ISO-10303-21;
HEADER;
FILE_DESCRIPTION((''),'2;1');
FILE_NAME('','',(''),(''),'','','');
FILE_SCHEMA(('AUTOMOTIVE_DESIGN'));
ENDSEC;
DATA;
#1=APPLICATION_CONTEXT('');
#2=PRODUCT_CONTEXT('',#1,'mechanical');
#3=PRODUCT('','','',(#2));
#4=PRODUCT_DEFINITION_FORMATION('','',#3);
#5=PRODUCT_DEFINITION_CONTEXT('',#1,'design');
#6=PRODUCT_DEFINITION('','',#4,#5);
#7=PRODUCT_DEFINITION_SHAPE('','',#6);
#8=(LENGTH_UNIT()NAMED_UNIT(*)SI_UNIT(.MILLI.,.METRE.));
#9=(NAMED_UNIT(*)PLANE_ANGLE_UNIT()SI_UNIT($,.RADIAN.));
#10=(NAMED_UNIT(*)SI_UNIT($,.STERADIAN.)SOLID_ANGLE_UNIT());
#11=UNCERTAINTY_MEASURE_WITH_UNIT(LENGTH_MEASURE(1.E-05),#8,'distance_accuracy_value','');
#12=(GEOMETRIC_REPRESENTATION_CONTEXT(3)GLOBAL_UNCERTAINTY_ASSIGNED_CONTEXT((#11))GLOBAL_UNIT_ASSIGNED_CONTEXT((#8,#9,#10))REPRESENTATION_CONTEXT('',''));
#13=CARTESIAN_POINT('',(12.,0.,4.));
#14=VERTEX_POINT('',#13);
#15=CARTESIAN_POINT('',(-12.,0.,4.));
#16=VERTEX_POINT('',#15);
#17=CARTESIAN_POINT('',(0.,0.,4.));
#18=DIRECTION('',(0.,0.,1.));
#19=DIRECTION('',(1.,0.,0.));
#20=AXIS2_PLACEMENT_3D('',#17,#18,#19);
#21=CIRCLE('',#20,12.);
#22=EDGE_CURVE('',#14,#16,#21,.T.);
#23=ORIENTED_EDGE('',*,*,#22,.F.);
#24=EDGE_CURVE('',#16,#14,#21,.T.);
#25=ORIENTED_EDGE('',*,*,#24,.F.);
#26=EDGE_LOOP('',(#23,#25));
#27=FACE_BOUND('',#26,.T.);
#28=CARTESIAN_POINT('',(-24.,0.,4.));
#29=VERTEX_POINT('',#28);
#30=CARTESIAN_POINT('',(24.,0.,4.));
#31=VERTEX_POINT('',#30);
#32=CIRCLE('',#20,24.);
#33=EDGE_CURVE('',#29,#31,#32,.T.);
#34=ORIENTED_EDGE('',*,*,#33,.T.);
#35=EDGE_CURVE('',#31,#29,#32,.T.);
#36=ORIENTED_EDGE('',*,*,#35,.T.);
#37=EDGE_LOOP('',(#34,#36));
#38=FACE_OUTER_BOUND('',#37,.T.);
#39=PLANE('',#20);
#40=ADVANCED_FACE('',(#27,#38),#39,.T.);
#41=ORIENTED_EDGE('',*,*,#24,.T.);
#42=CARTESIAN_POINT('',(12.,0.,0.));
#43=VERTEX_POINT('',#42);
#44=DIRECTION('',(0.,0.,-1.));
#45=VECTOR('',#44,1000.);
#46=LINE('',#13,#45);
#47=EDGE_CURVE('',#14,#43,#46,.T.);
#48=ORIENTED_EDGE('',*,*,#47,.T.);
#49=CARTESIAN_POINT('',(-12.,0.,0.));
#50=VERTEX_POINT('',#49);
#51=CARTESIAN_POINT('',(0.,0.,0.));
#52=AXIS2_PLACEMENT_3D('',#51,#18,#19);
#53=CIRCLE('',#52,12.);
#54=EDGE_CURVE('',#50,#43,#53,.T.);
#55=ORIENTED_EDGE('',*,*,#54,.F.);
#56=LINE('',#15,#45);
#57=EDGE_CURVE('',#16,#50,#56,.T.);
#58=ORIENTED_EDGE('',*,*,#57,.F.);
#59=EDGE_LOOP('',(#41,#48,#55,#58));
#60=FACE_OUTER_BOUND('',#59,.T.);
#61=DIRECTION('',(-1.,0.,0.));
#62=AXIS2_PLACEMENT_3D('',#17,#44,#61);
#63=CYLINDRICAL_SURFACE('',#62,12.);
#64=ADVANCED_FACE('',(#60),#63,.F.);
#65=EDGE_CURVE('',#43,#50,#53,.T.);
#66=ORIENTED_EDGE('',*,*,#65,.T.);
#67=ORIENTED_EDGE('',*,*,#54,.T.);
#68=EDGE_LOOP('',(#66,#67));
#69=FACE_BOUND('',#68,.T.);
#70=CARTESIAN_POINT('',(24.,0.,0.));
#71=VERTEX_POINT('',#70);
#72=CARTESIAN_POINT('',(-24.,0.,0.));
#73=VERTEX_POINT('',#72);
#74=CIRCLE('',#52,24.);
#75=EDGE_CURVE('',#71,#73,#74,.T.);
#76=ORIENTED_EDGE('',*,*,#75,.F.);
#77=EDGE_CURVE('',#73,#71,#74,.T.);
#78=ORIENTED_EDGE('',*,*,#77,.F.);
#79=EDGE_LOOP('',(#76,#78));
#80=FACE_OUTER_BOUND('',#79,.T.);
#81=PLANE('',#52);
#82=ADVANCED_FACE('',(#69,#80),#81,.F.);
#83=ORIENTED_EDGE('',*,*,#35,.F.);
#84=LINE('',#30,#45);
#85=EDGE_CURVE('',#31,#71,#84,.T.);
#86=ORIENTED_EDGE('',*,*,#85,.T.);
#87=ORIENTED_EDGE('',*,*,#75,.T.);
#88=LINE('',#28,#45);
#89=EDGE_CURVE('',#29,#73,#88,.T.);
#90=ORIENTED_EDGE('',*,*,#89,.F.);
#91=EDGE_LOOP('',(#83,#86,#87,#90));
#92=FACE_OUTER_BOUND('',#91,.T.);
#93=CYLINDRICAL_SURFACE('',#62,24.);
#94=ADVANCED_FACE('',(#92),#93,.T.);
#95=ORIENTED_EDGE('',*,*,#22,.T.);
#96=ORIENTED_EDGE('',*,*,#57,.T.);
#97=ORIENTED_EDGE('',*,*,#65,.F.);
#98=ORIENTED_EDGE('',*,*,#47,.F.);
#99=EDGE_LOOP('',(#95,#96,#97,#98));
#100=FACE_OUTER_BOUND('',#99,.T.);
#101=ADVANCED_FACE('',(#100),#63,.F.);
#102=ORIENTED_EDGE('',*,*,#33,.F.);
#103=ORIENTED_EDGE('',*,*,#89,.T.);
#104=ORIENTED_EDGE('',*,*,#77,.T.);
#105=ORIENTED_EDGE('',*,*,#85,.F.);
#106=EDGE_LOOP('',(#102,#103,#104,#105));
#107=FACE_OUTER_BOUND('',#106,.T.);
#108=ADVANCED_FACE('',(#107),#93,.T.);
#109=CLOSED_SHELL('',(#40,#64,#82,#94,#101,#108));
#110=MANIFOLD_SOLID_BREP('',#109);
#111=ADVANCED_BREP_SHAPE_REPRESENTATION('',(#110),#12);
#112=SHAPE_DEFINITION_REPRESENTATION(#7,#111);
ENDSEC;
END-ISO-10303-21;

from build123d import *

# Parameters (mm, degrees)
SKETCH1_R           = 24
SKETCH1_R_2         = 12
BOSS_EXTRUDE1_DEPTH = 4


with BuildPart() as part:
    # Sketch1 → Boss-Extrude1 (new body)
    with BuildSketch(Plane.XY):
        Circle(SKETCH1_R)
        Circle(SKETCH1_R_2, mode=Mode.SUBTRACT)
    extrude(amount=BOSS_EXTRUDE1_DEPTH)


solid = part.part
